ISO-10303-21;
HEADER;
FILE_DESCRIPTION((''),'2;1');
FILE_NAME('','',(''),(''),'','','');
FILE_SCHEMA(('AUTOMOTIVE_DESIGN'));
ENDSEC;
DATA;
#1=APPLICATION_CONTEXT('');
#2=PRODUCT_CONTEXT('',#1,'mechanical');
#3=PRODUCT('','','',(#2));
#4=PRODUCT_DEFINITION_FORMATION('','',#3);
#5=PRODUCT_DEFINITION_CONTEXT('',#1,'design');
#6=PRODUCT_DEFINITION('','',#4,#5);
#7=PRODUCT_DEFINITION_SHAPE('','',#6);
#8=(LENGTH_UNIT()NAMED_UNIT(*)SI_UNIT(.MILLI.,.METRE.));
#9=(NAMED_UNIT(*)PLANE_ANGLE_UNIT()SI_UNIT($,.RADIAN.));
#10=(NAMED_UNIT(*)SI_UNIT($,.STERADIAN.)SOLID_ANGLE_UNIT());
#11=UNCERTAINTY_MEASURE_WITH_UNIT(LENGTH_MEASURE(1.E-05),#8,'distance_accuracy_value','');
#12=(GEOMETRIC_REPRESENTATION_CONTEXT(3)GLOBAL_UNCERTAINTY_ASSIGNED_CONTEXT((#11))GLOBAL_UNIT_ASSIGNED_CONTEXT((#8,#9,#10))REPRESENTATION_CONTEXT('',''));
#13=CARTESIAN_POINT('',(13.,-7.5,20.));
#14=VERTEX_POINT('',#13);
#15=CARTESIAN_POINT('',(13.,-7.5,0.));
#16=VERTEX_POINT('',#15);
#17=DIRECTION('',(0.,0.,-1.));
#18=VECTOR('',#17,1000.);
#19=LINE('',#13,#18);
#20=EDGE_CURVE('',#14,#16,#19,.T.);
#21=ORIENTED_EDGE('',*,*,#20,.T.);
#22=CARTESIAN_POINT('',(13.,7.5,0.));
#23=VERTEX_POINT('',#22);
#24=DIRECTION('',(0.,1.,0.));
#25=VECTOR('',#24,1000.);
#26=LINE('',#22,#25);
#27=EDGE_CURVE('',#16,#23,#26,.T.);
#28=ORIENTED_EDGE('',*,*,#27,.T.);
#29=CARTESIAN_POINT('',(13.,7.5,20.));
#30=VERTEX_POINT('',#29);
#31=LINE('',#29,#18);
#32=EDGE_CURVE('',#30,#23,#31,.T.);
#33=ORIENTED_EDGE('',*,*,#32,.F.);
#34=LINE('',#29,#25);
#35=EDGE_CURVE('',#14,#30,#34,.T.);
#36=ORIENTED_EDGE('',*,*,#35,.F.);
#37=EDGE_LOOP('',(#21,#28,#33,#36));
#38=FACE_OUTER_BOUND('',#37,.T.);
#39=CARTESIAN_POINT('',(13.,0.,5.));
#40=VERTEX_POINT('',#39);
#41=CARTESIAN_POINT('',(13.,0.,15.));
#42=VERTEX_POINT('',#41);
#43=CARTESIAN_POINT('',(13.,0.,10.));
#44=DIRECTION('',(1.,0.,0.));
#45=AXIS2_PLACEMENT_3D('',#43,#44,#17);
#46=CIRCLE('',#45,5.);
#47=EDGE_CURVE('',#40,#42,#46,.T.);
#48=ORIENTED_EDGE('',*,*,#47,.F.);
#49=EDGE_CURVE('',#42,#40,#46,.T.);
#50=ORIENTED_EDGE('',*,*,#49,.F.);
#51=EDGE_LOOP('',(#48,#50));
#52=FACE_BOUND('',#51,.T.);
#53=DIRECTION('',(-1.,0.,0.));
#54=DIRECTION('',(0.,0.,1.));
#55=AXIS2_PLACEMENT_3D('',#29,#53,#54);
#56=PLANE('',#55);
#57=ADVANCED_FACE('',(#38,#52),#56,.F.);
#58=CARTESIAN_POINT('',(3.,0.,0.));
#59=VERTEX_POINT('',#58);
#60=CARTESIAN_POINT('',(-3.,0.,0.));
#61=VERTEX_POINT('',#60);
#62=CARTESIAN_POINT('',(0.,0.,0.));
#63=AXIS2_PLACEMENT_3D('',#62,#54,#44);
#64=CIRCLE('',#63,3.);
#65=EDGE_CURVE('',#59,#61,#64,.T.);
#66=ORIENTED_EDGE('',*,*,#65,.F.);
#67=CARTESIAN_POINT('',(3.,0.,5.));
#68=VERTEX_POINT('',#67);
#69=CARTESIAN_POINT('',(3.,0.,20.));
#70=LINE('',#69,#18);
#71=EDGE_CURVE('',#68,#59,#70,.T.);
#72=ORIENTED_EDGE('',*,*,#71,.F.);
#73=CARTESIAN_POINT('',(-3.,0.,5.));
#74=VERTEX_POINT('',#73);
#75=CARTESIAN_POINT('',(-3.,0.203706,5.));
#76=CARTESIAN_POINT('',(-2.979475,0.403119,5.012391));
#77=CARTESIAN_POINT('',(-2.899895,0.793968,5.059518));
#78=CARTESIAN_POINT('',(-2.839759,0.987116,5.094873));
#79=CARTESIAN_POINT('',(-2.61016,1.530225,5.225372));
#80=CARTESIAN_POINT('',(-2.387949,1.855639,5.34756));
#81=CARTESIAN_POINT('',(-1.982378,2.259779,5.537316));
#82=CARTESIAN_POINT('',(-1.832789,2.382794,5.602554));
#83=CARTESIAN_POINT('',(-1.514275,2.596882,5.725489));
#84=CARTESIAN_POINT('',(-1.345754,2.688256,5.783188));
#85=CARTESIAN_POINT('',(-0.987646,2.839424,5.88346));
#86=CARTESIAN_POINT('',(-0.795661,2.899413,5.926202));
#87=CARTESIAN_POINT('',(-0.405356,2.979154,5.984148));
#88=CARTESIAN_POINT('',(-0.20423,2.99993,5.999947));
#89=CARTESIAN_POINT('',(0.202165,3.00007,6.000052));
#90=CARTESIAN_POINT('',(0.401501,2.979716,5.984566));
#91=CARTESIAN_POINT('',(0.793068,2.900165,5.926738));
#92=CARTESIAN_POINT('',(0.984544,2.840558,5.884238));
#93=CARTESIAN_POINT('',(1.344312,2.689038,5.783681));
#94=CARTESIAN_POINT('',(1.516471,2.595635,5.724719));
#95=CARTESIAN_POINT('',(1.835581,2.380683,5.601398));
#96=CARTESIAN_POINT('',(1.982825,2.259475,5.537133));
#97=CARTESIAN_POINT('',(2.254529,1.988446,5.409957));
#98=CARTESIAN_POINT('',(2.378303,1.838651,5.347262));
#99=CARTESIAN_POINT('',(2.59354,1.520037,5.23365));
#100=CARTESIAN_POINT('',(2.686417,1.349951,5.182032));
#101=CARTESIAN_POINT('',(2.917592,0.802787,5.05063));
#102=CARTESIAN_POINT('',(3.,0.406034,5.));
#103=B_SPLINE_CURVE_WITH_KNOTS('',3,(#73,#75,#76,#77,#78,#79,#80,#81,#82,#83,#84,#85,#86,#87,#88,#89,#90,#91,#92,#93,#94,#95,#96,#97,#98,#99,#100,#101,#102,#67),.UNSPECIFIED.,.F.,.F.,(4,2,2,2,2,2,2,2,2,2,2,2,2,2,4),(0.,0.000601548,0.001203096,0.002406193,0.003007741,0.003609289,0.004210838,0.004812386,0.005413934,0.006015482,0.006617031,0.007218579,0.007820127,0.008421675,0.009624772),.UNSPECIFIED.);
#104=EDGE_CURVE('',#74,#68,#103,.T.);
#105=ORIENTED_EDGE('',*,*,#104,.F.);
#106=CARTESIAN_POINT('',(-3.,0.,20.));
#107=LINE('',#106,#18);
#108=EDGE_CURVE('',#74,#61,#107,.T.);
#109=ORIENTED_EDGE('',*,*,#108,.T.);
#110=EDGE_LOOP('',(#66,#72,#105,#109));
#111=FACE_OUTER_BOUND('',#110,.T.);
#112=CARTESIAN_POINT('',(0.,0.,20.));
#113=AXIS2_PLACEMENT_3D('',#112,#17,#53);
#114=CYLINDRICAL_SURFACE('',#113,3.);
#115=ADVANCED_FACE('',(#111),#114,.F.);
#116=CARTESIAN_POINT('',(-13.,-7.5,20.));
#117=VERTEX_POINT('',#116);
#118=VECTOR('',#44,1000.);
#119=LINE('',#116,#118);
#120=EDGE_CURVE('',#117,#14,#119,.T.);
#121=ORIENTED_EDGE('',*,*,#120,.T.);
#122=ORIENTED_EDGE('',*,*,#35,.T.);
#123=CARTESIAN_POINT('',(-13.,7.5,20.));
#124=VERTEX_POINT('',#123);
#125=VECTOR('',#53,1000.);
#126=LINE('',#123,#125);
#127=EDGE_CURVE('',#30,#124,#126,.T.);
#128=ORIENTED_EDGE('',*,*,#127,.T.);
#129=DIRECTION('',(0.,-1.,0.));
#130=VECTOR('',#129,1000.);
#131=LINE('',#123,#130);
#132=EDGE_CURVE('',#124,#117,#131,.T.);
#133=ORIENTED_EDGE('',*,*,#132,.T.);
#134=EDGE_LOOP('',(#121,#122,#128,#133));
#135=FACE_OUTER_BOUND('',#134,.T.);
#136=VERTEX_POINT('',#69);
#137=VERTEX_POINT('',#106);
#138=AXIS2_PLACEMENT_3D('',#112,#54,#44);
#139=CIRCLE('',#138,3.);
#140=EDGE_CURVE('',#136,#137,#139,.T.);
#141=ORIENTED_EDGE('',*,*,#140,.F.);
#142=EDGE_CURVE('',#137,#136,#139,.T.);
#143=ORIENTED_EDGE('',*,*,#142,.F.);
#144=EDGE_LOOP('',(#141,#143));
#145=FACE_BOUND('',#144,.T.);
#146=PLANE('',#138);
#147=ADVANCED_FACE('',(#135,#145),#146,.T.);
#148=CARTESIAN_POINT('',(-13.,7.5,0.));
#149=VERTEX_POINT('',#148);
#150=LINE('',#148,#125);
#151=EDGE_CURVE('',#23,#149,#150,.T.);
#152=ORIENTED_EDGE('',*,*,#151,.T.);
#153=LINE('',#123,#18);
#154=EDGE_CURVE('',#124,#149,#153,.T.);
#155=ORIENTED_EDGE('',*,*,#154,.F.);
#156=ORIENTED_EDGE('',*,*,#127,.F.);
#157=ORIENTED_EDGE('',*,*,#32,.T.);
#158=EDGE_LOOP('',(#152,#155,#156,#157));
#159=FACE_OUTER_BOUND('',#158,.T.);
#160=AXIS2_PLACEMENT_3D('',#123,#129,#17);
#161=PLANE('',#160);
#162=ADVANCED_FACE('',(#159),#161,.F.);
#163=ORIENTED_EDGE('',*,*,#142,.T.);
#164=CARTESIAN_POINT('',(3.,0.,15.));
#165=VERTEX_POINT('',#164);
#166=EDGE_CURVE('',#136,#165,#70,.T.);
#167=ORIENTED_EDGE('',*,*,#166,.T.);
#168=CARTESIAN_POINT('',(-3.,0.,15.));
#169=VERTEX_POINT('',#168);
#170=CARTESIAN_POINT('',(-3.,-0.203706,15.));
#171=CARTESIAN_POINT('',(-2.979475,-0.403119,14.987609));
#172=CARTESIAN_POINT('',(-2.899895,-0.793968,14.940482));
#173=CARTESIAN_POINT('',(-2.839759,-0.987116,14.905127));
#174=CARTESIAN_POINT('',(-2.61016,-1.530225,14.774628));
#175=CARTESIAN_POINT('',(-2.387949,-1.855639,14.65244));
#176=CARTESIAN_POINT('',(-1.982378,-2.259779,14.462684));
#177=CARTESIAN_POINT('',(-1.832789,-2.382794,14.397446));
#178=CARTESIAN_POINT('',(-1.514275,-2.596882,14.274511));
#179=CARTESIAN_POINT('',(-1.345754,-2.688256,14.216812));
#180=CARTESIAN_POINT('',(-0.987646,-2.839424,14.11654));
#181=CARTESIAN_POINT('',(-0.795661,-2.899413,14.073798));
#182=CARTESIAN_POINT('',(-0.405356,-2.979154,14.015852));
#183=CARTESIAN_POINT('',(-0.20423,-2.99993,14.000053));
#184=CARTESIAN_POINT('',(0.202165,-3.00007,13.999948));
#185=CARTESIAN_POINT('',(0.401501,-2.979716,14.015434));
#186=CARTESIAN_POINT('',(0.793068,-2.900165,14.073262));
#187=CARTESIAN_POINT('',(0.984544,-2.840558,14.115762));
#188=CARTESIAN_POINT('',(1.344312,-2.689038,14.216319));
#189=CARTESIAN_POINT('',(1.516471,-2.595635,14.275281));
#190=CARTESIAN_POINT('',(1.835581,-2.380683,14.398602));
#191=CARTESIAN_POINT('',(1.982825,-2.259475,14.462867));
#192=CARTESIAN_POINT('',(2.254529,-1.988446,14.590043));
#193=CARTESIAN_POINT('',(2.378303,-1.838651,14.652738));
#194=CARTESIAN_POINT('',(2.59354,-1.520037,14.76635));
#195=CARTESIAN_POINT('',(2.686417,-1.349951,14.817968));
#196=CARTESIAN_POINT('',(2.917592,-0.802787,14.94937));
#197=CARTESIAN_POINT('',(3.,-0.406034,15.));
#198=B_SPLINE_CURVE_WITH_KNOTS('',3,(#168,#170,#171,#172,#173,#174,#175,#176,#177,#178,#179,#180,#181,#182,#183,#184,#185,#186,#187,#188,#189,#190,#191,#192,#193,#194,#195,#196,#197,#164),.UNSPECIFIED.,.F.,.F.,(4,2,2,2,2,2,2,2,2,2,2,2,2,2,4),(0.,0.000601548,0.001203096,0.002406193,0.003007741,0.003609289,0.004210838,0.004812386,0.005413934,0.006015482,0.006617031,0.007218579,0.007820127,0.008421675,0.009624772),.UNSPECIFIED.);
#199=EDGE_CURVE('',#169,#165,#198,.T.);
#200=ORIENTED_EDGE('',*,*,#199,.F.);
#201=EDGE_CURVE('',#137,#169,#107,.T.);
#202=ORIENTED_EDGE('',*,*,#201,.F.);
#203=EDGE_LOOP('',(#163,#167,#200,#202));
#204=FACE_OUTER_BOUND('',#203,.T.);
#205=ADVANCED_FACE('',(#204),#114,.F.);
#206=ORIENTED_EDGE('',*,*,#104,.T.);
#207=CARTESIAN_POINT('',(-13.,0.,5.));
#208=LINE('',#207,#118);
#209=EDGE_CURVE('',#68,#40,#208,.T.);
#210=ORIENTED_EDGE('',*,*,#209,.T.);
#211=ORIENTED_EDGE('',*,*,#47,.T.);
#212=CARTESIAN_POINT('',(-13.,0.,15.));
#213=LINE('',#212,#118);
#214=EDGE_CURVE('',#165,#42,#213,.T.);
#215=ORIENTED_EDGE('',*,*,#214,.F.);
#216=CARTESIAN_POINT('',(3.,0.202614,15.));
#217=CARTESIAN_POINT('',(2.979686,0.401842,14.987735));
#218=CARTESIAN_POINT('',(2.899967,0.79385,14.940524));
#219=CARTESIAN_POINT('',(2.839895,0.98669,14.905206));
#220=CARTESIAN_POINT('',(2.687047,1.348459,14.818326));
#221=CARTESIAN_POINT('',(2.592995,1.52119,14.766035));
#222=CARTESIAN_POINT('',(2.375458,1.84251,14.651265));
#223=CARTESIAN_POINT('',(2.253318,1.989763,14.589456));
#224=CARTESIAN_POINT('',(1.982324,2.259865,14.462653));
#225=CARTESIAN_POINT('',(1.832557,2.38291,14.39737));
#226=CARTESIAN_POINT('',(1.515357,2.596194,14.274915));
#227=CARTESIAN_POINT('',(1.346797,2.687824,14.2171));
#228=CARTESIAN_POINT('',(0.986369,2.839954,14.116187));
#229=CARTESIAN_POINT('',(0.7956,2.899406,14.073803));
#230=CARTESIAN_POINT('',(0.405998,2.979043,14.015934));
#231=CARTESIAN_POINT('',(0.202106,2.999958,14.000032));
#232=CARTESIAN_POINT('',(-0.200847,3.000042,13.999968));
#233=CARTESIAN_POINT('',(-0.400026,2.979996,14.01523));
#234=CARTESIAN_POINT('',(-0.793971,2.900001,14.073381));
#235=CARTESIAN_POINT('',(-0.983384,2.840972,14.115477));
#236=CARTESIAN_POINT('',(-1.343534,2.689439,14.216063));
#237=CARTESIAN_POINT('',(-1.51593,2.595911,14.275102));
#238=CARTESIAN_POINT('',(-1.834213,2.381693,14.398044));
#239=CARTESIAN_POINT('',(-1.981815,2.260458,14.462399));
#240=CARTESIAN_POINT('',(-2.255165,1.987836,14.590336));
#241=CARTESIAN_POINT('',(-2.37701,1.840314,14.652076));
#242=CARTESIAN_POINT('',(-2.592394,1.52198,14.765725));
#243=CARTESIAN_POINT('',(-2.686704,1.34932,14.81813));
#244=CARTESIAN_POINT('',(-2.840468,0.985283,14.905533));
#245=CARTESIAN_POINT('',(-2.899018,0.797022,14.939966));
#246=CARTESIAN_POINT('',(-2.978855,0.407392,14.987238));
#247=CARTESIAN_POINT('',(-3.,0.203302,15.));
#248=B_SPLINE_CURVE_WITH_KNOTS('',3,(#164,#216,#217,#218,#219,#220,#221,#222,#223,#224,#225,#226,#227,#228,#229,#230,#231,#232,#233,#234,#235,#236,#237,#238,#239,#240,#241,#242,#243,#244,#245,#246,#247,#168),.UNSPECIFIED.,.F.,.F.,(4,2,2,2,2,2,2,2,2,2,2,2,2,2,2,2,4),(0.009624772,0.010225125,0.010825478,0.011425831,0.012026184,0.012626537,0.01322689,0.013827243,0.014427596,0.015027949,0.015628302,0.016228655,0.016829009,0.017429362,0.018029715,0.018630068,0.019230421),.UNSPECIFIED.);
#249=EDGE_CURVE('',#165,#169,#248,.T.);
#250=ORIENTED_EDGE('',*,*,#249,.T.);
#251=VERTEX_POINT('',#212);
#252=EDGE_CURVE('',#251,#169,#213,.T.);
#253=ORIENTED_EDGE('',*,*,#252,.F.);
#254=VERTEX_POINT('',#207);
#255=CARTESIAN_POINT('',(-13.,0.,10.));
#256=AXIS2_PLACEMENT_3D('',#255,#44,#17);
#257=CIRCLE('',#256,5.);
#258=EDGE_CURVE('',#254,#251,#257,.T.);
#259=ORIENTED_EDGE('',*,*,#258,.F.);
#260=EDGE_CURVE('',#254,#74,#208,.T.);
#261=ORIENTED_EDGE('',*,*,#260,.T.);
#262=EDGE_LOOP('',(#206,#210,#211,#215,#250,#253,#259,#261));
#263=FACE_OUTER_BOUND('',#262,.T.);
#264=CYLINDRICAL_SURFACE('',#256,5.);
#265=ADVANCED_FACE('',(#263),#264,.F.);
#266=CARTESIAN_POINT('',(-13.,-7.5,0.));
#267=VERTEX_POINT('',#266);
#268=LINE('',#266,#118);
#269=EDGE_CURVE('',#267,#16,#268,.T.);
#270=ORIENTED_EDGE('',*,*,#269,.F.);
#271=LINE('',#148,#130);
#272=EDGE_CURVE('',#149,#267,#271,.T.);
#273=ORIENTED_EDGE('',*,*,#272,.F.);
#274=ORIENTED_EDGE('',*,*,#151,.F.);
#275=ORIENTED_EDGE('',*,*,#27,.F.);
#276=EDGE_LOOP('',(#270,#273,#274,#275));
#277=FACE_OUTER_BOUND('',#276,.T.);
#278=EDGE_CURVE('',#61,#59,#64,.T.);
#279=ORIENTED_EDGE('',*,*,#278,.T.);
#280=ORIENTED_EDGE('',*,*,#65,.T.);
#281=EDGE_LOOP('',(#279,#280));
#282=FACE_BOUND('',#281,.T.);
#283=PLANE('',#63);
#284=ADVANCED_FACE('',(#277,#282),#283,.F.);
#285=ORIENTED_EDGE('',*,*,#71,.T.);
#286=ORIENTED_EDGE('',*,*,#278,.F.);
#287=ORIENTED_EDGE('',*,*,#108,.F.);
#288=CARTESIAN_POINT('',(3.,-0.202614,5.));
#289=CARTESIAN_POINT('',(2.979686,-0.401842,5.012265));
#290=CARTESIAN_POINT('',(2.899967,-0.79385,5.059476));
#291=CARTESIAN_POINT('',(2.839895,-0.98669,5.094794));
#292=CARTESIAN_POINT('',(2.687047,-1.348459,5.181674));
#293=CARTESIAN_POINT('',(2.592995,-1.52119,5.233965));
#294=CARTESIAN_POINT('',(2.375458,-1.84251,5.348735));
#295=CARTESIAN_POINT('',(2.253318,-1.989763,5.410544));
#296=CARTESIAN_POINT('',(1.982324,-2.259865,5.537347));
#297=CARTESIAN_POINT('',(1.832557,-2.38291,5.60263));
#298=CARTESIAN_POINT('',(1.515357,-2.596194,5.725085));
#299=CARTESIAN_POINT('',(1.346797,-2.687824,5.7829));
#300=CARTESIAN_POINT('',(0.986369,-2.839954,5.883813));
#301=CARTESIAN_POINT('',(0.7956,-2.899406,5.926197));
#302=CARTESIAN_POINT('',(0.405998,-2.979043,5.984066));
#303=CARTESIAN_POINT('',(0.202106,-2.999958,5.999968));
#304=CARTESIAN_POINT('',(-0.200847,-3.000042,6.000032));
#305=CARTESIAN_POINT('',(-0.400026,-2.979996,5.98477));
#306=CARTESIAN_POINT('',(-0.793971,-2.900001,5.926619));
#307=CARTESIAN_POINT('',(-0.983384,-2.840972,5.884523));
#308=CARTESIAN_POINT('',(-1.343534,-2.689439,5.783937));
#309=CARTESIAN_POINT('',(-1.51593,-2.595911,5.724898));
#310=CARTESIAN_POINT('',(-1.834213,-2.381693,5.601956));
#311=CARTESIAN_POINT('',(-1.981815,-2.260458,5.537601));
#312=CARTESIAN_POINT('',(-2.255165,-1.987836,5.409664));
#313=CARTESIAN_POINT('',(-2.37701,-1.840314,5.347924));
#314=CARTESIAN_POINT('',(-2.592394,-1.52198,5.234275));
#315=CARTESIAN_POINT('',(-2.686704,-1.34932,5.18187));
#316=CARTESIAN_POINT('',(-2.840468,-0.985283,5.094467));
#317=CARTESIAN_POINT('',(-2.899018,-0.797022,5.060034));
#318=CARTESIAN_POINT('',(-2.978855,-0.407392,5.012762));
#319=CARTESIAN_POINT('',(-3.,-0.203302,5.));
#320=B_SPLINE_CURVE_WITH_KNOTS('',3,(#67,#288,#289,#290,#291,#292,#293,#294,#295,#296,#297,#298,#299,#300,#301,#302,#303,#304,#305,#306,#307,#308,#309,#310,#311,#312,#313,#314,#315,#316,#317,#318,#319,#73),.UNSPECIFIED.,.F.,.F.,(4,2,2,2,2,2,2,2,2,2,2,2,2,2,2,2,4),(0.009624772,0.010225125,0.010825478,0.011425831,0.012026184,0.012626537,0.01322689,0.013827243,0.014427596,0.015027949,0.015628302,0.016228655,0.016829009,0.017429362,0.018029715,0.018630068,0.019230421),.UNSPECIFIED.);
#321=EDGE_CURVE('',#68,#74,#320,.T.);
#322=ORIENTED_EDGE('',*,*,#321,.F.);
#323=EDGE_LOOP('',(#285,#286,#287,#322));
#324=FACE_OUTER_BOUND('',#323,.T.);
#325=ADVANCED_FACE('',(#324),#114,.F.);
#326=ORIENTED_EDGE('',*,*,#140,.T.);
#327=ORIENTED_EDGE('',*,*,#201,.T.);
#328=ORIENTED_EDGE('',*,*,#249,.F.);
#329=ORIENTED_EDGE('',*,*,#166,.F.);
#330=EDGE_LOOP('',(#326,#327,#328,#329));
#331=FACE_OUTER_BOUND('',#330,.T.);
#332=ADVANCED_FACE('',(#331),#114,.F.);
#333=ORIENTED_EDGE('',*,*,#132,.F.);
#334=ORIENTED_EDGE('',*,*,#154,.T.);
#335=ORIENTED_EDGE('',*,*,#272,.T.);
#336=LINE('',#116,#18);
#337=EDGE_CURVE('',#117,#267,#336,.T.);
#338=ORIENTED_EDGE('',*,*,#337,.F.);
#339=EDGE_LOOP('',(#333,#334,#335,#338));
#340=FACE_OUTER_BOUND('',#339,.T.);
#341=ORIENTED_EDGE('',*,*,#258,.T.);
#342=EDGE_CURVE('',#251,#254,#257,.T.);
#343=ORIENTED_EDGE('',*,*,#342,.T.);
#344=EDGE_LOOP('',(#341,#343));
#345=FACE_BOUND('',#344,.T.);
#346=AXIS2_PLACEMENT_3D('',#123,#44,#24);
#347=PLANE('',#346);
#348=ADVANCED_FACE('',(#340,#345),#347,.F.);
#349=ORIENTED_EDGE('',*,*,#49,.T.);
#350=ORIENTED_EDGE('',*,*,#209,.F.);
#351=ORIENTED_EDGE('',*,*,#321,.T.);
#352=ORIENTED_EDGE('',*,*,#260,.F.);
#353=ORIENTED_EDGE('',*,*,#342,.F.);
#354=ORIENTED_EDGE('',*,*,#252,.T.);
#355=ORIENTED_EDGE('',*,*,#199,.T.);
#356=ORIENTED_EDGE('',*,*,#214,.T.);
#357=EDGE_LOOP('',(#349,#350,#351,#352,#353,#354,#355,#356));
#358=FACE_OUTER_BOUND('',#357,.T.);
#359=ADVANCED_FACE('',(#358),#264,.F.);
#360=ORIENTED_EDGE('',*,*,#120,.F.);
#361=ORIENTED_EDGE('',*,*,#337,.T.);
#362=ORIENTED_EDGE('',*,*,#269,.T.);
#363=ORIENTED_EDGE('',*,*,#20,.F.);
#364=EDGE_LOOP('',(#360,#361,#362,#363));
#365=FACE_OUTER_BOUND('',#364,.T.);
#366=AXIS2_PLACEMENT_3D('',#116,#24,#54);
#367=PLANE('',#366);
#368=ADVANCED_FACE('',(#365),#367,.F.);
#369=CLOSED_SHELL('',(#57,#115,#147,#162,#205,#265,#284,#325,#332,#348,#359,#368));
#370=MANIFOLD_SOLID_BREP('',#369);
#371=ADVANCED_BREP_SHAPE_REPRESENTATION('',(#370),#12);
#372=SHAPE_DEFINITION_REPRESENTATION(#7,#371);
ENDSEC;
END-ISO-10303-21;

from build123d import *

# Parameters (mm, degrees)
SKETCH1_W           = 26
SKETCH1_H           = 15
SKETCH1_R           = 3
BOSS_EXTRUDE1_DEPTH = 20
SKETCH2_R           = 5
CUT_EXTRUDE1_DEPTH  = 34.648922717


with BuildPart() as part:
    # Sketch1 → Boss-Extrude1 (new body)
    with BuildSketch(Plane.XY):
        Rectangle(SKETCH1_W, SKETCH1_H)
        Circle(SKETCH1_R, mode=Mode.SUBTRACT)
    extrude(amount=BOSS_EXTRUDE1_DEPTH)

    # Sketch2 → Cut-Extrude1 (cut, through all)
    with BuildSketch(Plane(origin=(13, 0, 0), x_dir=(0, 0, -1), z_dir=(1, 0, 0))):
        with Locations((-10, 0)):
            Circle(SKETCH2_R)
    extrude(amount=-CUT_EXTRUDE1_DEPTH, mode=Mode.SUBTRACT)


solid = part.part
